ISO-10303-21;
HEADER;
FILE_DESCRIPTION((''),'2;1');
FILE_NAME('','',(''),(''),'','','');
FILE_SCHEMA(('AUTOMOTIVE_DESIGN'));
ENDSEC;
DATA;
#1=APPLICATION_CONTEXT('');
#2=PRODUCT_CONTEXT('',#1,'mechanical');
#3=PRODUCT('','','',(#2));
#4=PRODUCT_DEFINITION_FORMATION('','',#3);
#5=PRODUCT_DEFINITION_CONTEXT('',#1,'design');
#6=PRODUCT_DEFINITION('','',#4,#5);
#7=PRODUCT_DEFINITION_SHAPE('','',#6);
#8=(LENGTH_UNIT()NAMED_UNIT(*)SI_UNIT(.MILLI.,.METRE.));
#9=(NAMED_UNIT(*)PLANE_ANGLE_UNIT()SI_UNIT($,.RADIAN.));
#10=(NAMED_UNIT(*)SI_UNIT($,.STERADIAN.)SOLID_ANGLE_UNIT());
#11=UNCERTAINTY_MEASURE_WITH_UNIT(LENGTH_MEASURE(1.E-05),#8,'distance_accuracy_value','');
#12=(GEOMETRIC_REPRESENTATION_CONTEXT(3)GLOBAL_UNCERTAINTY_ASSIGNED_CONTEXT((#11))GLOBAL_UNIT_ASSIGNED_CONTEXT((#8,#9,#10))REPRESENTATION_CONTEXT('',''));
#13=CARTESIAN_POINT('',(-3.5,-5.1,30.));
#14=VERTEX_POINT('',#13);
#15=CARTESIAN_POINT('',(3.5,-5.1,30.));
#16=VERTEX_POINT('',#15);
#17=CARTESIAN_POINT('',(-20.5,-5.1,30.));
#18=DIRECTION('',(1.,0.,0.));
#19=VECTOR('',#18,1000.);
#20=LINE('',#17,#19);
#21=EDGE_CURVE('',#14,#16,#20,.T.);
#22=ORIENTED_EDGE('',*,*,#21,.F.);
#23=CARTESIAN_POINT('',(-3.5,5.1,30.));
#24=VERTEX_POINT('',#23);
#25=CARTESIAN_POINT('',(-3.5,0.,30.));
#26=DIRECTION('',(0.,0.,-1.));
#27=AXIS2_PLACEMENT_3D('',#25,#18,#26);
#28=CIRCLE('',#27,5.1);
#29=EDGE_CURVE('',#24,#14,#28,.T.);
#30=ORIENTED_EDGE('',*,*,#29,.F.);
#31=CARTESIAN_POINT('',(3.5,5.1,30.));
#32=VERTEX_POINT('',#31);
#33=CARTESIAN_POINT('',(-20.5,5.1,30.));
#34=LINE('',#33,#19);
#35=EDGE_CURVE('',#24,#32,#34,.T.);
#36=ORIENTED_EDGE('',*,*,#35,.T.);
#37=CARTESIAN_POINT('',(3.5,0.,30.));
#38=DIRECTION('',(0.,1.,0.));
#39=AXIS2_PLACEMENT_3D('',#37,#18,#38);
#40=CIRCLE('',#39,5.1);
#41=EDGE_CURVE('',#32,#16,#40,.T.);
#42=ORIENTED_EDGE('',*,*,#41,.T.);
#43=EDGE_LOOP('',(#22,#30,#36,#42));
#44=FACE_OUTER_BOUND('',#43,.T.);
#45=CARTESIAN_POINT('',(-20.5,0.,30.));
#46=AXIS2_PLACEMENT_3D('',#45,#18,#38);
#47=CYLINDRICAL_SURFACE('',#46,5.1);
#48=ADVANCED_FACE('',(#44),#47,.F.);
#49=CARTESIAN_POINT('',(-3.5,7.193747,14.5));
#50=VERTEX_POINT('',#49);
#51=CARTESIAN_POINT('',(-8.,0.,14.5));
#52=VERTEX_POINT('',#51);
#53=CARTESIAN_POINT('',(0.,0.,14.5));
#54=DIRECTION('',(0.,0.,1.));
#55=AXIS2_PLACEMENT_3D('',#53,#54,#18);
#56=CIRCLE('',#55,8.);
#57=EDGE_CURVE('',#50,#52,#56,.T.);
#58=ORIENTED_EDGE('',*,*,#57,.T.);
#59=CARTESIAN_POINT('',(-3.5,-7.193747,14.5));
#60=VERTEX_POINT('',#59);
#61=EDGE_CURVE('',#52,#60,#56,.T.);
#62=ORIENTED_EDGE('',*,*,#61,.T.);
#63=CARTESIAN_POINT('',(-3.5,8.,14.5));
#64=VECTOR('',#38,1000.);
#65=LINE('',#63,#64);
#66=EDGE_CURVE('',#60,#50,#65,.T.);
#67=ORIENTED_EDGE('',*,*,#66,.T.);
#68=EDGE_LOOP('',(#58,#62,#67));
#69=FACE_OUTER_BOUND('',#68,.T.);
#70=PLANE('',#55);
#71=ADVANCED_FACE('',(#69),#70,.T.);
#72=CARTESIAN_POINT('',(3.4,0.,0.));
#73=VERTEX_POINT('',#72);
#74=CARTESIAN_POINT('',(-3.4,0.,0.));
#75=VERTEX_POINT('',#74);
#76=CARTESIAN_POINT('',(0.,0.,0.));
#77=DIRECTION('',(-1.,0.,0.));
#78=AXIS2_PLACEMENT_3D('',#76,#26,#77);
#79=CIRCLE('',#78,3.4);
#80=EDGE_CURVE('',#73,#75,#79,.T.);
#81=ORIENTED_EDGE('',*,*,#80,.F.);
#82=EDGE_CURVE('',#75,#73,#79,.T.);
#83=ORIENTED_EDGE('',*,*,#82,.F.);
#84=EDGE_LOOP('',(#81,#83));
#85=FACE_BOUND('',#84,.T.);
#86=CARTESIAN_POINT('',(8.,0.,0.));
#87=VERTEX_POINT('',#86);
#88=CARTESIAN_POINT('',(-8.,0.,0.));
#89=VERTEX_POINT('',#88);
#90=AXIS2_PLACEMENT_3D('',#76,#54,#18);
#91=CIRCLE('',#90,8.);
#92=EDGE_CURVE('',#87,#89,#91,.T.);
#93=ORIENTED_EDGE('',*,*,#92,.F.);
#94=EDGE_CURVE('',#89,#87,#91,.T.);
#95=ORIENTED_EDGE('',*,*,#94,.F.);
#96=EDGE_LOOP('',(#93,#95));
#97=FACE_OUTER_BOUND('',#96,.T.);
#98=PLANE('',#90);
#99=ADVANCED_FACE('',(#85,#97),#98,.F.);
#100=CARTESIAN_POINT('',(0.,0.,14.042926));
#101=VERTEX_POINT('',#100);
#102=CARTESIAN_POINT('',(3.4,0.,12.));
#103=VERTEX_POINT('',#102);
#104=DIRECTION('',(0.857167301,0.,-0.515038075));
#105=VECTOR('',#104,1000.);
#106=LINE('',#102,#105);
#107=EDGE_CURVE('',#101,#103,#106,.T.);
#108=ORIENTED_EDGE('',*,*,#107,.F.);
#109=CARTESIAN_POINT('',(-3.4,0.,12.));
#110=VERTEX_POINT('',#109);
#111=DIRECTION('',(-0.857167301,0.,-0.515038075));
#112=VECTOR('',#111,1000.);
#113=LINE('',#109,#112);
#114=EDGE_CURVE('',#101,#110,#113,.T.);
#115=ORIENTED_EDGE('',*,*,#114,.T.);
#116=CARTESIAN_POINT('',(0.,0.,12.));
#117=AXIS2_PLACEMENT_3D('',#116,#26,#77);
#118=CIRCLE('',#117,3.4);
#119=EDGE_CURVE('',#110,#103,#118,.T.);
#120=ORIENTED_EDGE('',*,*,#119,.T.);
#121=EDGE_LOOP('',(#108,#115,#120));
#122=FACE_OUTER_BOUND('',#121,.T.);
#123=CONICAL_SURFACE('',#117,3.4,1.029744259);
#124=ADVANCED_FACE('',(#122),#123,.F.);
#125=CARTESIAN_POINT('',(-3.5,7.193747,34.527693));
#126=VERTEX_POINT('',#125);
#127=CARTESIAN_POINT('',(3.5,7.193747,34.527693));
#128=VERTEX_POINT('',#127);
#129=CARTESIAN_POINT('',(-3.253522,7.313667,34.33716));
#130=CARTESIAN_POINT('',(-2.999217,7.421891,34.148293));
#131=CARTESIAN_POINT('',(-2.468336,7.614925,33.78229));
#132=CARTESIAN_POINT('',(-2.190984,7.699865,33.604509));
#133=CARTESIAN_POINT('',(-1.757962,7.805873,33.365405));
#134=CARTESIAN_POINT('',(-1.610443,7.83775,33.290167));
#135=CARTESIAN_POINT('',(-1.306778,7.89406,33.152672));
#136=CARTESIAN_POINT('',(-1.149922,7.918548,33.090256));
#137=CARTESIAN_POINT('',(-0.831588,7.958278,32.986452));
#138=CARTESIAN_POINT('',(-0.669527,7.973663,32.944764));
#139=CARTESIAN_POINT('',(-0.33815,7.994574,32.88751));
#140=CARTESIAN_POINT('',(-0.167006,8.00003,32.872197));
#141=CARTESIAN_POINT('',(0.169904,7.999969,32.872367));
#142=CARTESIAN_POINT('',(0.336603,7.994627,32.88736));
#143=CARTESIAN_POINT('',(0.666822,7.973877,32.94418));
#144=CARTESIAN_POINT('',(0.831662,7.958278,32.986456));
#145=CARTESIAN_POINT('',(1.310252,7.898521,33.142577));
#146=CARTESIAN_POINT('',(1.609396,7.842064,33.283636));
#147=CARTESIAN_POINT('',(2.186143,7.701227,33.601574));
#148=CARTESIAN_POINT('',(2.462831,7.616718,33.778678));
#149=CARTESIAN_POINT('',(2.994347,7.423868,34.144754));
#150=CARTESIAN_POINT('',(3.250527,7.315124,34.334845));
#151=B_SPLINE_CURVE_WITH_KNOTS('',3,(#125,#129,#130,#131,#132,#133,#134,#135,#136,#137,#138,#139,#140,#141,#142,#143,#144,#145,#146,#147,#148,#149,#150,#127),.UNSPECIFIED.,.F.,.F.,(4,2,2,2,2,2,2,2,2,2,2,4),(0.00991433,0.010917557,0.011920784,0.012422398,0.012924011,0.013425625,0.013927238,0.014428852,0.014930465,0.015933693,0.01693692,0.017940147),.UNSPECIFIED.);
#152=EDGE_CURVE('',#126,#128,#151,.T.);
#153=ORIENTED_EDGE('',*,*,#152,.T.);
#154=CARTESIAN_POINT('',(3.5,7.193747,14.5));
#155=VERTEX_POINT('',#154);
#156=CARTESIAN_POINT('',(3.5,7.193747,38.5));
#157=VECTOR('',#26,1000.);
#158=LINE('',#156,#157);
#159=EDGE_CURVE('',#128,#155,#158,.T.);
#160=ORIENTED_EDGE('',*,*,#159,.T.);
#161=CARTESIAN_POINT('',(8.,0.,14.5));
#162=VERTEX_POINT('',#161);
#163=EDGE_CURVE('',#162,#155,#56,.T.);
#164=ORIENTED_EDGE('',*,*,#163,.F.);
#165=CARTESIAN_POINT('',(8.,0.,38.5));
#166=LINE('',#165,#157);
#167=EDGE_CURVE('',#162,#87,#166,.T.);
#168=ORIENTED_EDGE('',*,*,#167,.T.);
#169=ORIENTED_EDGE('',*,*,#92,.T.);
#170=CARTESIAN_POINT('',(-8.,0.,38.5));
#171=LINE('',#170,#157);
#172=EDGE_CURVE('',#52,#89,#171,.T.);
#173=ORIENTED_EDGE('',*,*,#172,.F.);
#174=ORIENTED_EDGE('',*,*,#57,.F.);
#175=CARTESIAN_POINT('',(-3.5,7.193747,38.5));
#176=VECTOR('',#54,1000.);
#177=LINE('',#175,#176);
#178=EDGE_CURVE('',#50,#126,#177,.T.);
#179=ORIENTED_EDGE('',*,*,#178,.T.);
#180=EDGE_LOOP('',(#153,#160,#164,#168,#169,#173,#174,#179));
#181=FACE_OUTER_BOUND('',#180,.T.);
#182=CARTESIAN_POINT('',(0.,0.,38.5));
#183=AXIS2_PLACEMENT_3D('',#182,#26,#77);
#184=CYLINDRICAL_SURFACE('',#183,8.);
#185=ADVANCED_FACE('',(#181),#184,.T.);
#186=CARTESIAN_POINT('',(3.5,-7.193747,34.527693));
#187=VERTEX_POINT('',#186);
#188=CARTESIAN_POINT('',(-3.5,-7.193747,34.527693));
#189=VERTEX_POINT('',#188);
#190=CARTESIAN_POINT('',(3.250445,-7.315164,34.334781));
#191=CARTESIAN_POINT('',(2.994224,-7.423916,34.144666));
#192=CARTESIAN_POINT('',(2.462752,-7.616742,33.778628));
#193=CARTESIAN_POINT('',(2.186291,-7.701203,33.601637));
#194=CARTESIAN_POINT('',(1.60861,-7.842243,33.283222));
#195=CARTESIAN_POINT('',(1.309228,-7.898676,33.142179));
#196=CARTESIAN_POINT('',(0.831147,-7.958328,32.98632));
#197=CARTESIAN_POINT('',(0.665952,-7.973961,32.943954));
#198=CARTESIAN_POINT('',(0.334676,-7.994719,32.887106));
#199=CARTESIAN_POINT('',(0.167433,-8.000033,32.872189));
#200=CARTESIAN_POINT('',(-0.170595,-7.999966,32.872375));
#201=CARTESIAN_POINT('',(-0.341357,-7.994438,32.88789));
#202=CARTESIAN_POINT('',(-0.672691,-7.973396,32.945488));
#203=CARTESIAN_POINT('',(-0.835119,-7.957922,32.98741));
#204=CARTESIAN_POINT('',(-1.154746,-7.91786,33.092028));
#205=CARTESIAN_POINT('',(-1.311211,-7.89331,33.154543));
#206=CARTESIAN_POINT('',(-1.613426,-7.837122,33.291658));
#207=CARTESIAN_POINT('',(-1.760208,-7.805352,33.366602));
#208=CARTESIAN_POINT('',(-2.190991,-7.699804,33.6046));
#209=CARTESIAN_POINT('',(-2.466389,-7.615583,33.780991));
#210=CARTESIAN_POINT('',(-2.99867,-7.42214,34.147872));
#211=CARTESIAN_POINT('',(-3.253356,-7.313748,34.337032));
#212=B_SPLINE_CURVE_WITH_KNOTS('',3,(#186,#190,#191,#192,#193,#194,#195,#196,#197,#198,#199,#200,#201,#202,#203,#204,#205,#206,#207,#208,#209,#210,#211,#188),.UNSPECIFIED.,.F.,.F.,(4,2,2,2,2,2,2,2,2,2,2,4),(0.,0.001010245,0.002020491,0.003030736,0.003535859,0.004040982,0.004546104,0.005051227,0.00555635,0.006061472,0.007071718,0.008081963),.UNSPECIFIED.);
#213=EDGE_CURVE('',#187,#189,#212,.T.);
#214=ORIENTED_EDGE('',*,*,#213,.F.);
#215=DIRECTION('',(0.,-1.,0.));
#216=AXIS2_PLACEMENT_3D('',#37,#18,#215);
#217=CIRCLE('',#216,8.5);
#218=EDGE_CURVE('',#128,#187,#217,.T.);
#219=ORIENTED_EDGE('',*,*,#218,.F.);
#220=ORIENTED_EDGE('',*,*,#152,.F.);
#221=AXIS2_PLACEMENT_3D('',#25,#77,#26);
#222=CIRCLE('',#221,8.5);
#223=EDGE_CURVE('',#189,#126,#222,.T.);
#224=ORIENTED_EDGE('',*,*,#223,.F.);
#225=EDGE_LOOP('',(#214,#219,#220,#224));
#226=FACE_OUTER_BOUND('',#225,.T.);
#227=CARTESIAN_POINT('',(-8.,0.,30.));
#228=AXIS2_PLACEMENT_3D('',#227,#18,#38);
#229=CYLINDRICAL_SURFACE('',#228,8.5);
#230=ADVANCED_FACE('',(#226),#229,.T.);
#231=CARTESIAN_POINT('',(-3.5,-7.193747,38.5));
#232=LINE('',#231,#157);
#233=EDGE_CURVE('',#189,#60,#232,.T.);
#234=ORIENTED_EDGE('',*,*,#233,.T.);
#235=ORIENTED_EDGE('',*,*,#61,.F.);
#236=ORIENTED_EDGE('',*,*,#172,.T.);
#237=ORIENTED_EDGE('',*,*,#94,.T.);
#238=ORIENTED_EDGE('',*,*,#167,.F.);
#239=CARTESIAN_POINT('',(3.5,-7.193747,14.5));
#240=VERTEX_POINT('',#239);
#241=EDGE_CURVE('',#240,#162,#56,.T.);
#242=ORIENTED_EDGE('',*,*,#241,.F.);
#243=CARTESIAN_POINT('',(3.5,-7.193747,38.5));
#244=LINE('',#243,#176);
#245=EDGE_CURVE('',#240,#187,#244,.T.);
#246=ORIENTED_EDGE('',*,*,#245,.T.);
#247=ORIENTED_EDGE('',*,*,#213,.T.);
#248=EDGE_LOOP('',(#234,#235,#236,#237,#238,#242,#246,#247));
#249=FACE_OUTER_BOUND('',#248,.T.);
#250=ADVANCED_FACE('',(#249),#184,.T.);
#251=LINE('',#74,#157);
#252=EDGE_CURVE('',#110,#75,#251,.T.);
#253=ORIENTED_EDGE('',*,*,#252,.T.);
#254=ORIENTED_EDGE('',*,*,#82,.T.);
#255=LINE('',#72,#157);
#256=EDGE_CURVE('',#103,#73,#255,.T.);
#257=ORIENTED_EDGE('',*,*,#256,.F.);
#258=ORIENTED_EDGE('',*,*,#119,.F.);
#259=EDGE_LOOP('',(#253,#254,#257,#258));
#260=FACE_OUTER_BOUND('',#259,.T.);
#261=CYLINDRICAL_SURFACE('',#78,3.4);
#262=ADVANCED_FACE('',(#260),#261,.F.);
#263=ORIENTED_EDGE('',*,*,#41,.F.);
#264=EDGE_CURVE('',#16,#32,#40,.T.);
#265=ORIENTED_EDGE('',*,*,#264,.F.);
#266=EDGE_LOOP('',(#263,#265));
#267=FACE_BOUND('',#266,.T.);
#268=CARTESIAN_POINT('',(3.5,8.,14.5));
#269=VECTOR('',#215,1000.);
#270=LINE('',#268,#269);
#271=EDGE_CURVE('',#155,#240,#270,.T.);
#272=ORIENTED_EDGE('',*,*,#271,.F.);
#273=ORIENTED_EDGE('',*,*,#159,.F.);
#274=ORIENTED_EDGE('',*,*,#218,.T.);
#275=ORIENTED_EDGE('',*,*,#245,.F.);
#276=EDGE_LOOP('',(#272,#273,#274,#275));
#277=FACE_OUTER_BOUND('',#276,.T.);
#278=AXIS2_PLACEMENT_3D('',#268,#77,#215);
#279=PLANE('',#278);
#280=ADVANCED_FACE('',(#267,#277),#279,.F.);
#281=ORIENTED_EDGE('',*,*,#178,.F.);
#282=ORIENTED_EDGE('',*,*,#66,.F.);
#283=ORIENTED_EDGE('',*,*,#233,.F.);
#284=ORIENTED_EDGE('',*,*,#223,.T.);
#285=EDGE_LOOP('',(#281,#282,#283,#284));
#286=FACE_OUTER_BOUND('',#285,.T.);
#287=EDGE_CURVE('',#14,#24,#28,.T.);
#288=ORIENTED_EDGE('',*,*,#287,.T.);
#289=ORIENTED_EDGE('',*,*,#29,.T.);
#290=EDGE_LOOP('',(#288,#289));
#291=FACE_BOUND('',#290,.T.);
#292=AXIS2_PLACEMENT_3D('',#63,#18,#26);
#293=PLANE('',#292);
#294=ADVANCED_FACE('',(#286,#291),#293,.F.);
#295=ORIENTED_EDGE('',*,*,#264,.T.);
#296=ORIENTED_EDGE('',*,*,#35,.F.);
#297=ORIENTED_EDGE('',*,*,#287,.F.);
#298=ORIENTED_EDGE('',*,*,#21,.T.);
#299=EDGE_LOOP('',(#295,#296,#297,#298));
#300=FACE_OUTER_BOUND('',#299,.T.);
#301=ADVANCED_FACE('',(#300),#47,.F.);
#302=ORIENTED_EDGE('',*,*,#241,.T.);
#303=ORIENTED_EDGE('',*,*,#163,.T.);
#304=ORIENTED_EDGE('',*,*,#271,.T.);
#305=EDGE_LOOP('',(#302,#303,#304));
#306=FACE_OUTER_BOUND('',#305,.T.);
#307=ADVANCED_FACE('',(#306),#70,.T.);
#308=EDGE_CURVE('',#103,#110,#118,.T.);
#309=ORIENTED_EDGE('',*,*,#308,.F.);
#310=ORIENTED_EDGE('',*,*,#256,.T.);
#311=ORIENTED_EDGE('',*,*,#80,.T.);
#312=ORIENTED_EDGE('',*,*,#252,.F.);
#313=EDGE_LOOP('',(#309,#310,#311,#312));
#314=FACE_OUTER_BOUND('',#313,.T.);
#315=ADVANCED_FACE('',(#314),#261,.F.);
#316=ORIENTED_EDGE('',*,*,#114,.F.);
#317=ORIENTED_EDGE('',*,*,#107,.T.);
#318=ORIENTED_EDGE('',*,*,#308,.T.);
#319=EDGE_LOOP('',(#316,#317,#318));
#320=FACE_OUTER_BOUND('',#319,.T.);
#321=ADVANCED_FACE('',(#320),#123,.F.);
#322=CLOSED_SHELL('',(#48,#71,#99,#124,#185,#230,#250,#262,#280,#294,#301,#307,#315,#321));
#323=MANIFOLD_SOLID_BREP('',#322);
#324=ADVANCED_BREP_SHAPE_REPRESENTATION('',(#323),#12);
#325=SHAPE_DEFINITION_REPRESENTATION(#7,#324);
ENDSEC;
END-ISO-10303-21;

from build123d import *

# Parameters (mm, degrees)
SKETCH_1_R             = 8
EXTRUDE_1_DEPTH        = 38.5
SKETCH_2_W             = 5
SKETCH_2_H             = 16
CUT_EXTRUDE_1_DEPTH    = 24
SKETCH_3_R             = 5.1
CUT_EXTRUDE_2_DEPTH    = 24
CUT_EXTRUDE_3_DEPTH    = 41.969500851
HOLE_WIZARD_M8_1_D     = 6.8
HOLE_WIZARD_M8_1_DEPTH = 12
HOLE_WIZARD_M8_1_TIP   = 2.042926105


with BuildPart() as part:
    # 草图1 → 凸台-拉伸1 (new body)
    with BuildSketch(Plane.XY):
        Circle(SKETCH_1_R)
    extrude(amount=EXTRUDE_1_DEPTH)

    # 草图2 → 切除-拉伸1 (cut)
    with BuildSketch(Plane.XY.offset(38.5)):
        with Locations((6, 0)):
            Rectangle(SKETCH_2_W, SKETCH_2_H)
        with Locations((-6, 0)):
            Rectangle(SKETCH_2_W, SKETCH_2_H)
    extrude(amount=-CUT_EXTRUDE_1_DEPTH, mode=Mode.SUBTRACT)

    # 草图3 → 切除-拉伸2 (cut)
    with BuildSketch(Plane(origin=(3.5, 0, 0), x_dir=(0, 0, -1), z_dir=(1, 0, 0))):
        with Locations(Location((-30, 0, 0), (0, 0, 90))):
            Circle(SKETCH_3_R)
    extrude(amount=-CUT_EXTRUDE_2_DEPTH, mode=Mode.SUBTRACT)

    # 草图4 → 切除-拉伸3 (cut, through all)
    with BuildSketch(Plane(origin=(3.5, 0, 0), x_dir=(0, 0, -1), z_dir=(1, 0, 0))):
        with BuildLine():
            Line((-30, 8.5), (-30, 11))
            Line((-30, 11), (-45, 11))
            Line((-45, 11), (-45, -11))
            Line((-45, -11), (-30, -11))
            Line((-30, -11), (-30, -8.5))
            ThreePointArc((-30, -8.5), (-38.5, 0), (-30, 8.5))
        make_face()
    extrude(amount=-CUT_EXTRUDE_3_DEPTH, mode=Mode.SUBTRACT)

    # M8 螺纹孔1
    with Locations(Plane(origin=(0, 0, 0), x_dir=(-1, 0, 0), z_dir=(0, 0, -1))):
        with Locations((0, 0)):
            Hole(HOLE_WIZARD_M8_1_D / 2, depth=HOLE_WIZARD_M8_1_DEPTH)
            with Locations((0, 0, -(HOLE_WIZARD_M8_1_DEPTH + HOLE_WIZARD_M8_1_TIP / 2))):  # 118° drill point
                Cone(0, HOLE_WIZARD_M8_1_D / 2, HOLE_WIZARD_M8_1_TIP, mode=Mode.SUBTRACT)


solid = part.part
